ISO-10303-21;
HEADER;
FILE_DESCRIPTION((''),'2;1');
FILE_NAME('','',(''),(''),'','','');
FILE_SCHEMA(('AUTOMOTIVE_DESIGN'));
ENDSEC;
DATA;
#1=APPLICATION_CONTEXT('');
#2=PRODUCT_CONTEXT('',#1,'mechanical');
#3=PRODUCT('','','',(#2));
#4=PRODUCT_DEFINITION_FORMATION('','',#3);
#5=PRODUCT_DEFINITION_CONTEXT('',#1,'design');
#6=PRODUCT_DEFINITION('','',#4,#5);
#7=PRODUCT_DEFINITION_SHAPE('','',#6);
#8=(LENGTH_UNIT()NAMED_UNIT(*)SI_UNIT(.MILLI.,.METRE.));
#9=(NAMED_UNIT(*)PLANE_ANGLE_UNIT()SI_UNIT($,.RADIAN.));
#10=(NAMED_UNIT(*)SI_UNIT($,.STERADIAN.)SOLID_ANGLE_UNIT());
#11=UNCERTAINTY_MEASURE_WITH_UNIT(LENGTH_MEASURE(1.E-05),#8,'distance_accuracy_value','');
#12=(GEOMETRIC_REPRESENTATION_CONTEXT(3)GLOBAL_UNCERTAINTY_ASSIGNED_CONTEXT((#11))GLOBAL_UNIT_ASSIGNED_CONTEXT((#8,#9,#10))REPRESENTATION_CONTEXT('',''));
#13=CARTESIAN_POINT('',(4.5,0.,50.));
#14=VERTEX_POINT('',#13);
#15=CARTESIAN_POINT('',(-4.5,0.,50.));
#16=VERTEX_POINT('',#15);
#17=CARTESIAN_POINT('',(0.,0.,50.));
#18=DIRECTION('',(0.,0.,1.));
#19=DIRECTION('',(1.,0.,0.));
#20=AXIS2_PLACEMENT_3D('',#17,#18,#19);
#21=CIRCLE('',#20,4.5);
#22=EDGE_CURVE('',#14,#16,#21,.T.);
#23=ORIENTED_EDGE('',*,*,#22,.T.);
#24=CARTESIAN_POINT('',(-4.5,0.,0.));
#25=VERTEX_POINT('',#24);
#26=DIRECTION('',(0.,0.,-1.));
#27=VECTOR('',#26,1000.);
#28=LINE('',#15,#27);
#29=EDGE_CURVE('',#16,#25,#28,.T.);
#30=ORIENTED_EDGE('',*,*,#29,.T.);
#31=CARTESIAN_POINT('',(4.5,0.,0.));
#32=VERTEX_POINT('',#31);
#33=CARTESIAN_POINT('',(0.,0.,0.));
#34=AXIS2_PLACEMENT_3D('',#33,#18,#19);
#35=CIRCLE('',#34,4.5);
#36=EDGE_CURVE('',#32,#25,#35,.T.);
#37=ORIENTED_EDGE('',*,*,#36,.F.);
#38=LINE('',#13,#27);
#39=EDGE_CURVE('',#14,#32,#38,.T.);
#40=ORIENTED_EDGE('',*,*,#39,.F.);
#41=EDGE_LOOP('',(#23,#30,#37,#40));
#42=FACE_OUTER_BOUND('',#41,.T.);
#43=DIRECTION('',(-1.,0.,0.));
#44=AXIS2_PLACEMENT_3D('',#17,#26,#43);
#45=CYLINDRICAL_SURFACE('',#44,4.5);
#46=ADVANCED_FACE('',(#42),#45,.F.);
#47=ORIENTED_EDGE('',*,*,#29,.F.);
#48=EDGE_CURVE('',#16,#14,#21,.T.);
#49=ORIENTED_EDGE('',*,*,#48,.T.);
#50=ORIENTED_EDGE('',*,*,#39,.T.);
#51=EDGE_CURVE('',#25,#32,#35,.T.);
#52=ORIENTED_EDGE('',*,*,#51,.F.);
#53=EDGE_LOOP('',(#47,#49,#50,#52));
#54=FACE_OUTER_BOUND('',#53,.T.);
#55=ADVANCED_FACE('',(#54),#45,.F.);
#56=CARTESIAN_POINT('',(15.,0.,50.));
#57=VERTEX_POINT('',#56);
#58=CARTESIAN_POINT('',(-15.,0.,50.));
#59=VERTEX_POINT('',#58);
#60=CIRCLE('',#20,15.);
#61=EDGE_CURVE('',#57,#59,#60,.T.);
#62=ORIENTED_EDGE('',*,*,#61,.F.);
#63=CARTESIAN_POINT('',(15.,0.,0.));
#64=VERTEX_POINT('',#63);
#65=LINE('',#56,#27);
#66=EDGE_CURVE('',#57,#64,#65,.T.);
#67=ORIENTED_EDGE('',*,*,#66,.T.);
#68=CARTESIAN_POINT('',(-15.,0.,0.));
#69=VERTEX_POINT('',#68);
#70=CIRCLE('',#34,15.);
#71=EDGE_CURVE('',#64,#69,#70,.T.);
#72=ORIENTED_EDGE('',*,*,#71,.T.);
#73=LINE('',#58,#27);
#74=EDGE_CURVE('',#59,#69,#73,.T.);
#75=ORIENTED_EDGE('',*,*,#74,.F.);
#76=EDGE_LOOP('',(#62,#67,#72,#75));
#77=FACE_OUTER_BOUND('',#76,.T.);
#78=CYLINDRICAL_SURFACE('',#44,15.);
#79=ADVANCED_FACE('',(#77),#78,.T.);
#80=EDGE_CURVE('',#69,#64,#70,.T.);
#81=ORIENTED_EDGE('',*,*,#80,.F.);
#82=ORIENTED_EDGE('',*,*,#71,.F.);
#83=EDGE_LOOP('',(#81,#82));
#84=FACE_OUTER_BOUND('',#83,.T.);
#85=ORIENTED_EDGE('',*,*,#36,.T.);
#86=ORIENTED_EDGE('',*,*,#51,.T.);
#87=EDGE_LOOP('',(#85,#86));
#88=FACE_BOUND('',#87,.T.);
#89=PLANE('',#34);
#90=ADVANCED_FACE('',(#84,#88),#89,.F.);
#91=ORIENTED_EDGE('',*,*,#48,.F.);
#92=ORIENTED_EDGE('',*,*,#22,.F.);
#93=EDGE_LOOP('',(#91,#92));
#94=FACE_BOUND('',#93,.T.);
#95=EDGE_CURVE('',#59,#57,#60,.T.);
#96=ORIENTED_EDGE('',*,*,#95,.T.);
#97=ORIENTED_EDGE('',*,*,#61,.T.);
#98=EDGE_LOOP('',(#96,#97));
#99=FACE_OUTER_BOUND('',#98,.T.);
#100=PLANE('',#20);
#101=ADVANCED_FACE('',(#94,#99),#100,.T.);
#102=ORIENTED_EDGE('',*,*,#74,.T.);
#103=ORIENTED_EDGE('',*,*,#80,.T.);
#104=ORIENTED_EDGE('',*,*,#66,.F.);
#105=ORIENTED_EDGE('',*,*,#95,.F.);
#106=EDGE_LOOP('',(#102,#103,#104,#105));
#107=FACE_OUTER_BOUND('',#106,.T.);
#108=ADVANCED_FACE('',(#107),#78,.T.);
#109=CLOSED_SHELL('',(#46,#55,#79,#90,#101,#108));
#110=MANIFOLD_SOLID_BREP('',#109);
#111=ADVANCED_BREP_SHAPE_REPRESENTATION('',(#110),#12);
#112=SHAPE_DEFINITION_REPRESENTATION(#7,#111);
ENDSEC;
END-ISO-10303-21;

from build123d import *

# Parameters (mm, degrees)
SKETCH_1_R      = 15
SKETCH_1_R_2    = 4.5
EXTRUDE_1_DEPTH = 50


with BuildPart() as part:
    # 草图1 → 凸台-拉伸1 (new body)
    with BuildSketch(Plane.XY):
        Circle(SKETCH_1_R)
        Circle(SKETCH_1_R_2, mode=Mode.SUBTRACT)
    extrude(amount=EXTRUDE_1_DEPTH)


solid = part.part
